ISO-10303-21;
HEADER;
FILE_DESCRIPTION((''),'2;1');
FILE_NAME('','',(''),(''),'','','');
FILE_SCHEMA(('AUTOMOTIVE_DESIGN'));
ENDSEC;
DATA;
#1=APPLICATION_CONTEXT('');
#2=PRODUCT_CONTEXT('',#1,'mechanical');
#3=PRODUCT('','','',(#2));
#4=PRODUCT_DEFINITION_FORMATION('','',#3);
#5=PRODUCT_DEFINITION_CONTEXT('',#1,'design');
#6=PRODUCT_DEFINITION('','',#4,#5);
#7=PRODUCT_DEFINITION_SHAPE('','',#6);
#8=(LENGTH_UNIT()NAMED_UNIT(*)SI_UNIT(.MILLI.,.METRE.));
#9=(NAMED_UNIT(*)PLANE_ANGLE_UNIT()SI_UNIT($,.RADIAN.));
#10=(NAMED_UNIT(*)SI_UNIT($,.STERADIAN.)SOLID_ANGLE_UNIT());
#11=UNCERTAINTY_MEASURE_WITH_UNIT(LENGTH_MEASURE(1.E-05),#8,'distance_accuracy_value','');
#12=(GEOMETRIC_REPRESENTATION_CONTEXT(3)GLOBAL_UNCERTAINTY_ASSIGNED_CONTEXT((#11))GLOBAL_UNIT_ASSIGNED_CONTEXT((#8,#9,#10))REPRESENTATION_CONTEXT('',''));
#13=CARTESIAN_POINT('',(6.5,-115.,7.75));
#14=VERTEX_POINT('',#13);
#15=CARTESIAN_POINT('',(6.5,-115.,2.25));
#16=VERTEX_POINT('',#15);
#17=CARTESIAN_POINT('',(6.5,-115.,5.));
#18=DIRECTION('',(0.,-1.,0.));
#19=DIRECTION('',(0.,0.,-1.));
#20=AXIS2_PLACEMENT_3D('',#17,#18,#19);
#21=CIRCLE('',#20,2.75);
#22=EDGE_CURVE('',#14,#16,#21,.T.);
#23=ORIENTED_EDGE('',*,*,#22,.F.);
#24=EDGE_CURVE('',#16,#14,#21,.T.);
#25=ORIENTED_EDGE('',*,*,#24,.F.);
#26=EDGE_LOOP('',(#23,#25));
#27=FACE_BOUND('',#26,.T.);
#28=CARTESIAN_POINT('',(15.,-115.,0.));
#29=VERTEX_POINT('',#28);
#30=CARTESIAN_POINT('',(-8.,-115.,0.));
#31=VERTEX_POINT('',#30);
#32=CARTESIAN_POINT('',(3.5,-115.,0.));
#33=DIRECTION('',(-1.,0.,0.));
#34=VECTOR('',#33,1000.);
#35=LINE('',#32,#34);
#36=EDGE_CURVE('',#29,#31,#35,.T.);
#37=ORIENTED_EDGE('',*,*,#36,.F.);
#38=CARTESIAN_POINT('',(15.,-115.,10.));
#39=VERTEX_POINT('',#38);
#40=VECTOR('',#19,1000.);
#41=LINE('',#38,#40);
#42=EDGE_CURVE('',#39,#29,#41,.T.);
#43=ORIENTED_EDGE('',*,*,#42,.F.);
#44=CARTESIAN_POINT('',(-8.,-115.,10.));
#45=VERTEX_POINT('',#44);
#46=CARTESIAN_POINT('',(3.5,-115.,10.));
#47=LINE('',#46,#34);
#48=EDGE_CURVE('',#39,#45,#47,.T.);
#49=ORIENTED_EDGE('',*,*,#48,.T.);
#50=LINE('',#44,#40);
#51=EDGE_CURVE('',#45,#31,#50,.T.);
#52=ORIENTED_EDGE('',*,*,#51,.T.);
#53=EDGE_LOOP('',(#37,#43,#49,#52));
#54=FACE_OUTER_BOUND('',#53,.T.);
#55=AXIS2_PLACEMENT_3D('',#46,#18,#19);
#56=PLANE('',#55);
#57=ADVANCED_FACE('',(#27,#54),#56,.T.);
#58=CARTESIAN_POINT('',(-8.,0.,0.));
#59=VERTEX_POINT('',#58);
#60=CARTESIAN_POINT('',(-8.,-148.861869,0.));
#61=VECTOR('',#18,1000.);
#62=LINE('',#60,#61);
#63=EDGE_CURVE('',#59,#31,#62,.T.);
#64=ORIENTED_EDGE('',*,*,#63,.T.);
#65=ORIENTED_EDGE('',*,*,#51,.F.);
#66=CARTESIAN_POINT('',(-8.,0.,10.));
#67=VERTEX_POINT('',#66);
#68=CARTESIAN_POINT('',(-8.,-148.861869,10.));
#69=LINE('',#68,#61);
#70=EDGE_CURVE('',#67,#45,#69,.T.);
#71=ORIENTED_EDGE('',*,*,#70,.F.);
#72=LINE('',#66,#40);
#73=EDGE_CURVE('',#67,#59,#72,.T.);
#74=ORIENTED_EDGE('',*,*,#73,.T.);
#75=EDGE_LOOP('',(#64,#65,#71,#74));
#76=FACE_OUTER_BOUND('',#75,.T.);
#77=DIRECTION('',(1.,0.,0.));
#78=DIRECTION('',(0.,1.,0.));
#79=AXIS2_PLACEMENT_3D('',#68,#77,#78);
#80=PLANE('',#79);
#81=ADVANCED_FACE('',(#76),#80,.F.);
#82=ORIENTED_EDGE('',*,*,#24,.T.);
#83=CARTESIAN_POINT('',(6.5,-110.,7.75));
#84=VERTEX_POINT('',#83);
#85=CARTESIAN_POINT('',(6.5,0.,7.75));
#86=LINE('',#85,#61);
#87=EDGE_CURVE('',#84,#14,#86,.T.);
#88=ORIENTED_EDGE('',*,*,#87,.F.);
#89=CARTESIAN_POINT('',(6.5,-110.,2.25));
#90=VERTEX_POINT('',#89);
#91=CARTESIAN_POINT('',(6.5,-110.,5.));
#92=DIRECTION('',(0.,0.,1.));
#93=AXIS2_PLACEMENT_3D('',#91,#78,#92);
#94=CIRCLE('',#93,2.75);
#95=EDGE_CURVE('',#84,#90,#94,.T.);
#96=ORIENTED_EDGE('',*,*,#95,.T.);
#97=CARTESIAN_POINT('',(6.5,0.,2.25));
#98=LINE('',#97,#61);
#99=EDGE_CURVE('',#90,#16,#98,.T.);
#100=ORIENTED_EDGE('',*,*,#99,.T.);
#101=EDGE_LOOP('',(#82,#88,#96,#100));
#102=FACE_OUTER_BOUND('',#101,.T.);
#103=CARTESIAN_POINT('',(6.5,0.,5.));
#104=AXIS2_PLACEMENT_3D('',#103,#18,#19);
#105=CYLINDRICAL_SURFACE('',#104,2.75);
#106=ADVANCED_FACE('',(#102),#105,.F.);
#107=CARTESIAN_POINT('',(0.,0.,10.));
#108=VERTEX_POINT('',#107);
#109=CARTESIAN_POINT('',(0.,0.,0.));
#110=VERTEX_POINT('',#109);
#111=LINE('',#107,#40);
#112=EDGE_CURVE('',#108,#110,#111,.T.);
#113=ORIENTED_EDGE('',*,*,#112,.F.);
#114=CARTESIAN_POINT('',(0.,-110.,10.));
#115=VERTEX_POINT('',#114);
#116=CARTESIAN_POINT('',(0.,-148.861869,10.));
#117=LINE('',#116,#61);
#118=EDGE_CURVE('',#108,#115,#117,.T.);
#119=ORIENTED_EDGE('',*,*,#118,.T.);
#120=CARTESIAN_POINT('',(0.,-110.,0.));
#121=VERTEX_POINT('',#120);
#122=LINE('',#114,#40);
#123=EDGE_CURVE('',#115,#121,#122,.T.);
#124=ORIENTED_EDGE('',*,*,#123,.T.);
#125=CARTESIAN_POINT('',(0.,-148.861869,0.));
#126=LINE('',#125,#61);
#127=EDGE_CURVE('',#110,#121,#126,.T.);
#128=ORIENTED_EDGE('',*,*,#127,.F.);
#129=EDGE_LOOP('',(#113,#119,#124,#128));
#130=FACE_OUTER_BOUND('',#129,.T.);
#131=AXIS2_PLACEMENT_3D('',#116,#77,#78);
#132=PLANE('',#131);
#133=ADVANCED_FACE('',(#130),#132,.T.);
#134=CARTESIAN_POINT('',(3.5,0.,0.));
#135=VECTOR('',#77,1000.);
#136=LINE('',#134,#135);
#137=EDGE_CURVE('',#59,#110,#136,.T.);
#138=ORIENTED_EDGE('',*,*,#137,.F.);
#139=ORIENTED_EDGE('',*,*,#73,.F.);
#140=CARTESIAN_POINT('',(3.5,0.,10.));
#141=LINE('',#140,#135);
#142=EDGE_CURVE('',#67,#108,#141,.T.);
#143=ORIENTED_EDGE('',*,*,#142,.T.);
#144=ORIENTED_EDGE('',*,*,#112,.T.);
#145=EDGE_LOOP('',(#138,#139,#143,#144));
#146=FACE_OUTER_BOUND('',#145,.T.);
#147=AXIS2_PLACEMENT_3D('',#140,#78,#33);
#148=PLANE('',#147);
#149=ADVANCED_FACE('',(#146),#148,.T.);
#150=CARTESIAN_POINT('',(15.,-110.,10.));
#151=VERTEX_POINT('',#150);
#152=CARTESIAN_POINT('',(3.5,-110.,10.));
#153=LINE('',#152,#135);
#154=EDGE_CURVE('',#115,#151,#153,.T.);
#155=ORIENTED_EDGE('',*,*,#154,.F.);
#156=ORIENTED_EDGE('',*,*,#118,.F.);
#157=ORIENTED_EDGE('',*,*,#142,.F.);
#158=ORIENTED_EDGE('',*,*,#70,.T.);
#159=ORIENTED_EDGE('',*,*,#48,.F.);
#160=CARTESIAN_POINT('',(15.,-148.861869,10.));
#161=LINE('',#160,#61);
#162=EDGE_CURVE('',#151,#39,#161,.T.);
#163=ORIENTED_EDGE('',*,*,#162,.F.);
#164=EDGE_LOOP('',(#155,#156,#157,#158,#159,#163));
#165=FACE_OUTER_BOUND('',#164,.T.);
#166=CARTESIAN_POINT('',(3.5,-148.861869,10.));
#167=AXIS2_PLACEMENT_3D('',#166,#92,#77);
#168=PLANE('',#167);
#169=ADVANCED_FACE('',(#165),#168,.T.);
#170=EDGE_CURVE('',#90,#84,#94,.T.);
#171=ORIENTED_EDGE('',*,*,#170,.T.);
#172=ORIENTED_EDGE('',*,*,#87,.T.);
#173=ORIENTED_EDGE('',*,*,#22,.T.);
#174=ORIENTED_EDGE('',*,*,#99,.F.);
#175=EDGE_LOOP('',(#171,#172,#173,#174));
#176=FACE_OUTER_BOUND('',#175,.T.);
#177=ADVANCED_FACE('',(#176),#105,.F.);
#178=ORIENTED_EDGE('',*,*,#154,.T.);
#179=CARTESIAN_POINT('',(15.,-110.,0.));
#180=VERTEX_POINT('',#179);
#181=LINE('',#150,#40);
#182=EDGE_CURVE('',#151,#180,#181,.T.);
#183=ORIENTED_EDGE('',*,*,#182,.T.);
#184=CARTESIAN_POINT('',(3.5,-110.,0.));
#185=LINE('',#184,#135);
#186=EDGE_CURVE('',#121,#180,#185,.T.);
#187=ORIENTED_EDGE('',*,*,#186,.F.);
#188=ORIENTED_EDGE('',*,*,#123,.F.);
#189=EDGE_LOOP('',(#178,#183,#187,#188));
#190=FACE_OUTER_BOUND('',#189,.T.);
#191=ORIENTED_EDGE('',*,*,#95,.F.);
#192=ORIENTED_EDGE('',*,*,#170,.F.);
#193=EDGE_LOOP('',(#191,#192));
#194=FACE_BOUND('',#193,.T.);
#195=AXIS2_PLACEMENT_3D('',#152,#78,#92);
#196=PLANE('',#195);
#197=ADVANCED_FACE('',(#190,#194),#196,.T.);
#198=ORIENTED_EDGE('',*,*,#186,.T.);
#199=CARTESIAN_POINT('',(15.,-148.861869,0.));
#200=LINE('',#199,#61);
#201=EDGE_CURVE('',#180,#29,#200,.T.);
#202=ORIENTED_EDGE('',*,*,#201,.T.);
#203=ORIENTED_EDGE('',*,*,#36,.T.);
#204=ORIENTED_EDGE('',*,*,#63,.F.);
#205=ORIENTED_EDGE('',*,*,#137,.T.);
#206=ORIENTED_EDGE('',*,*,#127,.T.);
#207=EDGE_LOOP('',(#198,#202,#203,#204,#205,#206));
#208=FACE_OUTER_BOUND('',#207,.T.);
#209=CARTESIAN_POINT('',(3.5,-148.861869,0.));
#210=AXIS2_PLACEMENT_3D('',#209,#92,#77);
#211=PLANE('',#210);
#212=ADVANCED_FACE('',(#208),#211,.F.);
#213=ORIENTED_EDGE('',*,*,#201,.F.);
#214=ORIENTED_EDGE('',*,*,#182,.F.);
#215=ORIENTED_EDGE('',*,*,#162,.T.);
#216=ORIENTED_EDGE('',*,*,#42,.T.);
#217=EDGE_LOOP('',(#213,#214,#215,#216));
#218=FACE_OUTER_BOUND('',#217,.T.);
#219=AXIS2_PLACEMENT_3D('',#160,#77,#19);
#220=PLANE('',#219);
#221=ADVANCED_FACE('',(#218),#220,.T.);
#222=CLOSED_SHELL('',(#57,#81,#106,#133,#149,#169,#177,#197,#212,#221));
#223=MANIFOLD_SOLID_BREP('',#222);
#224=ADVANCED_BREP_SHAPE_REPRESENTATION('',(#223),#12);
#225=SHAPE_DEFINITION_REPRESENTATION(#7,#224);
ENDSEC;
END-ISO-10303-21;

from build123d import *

# Parameters (mm, degrees)
EXTRUDE_1_DEPTH     = 10
SKETCH_2_R          = 2.75
CUT_EXTRUDE_1_DEPTH = 117.404467268


with BuildPart() as part:
    # 草图1 → 凸台-拉伸1 (new body)
    with BuildSketch(Plane.XY):
        Polygon((0, 0), (0, -110), (15, -110), (15, -115), (-8, -115), (-8, 0), align=None)
    extrude(amount=EXTRUDE_1_DEPTH)

    # 草图2 → 切除-拉伸1 (cut, through all)
    with BuildSketch(Plane.XZ.offset(115)):
        with Locations(Location((6.5, 5, 0), (0, 0, 270))):
            Circle(SKETCH_2_R)
    extrude(amount=-CUT_EXTRUDE_1_DEPTH, mode=Mode.SUBTRACT)


solid = part.part
